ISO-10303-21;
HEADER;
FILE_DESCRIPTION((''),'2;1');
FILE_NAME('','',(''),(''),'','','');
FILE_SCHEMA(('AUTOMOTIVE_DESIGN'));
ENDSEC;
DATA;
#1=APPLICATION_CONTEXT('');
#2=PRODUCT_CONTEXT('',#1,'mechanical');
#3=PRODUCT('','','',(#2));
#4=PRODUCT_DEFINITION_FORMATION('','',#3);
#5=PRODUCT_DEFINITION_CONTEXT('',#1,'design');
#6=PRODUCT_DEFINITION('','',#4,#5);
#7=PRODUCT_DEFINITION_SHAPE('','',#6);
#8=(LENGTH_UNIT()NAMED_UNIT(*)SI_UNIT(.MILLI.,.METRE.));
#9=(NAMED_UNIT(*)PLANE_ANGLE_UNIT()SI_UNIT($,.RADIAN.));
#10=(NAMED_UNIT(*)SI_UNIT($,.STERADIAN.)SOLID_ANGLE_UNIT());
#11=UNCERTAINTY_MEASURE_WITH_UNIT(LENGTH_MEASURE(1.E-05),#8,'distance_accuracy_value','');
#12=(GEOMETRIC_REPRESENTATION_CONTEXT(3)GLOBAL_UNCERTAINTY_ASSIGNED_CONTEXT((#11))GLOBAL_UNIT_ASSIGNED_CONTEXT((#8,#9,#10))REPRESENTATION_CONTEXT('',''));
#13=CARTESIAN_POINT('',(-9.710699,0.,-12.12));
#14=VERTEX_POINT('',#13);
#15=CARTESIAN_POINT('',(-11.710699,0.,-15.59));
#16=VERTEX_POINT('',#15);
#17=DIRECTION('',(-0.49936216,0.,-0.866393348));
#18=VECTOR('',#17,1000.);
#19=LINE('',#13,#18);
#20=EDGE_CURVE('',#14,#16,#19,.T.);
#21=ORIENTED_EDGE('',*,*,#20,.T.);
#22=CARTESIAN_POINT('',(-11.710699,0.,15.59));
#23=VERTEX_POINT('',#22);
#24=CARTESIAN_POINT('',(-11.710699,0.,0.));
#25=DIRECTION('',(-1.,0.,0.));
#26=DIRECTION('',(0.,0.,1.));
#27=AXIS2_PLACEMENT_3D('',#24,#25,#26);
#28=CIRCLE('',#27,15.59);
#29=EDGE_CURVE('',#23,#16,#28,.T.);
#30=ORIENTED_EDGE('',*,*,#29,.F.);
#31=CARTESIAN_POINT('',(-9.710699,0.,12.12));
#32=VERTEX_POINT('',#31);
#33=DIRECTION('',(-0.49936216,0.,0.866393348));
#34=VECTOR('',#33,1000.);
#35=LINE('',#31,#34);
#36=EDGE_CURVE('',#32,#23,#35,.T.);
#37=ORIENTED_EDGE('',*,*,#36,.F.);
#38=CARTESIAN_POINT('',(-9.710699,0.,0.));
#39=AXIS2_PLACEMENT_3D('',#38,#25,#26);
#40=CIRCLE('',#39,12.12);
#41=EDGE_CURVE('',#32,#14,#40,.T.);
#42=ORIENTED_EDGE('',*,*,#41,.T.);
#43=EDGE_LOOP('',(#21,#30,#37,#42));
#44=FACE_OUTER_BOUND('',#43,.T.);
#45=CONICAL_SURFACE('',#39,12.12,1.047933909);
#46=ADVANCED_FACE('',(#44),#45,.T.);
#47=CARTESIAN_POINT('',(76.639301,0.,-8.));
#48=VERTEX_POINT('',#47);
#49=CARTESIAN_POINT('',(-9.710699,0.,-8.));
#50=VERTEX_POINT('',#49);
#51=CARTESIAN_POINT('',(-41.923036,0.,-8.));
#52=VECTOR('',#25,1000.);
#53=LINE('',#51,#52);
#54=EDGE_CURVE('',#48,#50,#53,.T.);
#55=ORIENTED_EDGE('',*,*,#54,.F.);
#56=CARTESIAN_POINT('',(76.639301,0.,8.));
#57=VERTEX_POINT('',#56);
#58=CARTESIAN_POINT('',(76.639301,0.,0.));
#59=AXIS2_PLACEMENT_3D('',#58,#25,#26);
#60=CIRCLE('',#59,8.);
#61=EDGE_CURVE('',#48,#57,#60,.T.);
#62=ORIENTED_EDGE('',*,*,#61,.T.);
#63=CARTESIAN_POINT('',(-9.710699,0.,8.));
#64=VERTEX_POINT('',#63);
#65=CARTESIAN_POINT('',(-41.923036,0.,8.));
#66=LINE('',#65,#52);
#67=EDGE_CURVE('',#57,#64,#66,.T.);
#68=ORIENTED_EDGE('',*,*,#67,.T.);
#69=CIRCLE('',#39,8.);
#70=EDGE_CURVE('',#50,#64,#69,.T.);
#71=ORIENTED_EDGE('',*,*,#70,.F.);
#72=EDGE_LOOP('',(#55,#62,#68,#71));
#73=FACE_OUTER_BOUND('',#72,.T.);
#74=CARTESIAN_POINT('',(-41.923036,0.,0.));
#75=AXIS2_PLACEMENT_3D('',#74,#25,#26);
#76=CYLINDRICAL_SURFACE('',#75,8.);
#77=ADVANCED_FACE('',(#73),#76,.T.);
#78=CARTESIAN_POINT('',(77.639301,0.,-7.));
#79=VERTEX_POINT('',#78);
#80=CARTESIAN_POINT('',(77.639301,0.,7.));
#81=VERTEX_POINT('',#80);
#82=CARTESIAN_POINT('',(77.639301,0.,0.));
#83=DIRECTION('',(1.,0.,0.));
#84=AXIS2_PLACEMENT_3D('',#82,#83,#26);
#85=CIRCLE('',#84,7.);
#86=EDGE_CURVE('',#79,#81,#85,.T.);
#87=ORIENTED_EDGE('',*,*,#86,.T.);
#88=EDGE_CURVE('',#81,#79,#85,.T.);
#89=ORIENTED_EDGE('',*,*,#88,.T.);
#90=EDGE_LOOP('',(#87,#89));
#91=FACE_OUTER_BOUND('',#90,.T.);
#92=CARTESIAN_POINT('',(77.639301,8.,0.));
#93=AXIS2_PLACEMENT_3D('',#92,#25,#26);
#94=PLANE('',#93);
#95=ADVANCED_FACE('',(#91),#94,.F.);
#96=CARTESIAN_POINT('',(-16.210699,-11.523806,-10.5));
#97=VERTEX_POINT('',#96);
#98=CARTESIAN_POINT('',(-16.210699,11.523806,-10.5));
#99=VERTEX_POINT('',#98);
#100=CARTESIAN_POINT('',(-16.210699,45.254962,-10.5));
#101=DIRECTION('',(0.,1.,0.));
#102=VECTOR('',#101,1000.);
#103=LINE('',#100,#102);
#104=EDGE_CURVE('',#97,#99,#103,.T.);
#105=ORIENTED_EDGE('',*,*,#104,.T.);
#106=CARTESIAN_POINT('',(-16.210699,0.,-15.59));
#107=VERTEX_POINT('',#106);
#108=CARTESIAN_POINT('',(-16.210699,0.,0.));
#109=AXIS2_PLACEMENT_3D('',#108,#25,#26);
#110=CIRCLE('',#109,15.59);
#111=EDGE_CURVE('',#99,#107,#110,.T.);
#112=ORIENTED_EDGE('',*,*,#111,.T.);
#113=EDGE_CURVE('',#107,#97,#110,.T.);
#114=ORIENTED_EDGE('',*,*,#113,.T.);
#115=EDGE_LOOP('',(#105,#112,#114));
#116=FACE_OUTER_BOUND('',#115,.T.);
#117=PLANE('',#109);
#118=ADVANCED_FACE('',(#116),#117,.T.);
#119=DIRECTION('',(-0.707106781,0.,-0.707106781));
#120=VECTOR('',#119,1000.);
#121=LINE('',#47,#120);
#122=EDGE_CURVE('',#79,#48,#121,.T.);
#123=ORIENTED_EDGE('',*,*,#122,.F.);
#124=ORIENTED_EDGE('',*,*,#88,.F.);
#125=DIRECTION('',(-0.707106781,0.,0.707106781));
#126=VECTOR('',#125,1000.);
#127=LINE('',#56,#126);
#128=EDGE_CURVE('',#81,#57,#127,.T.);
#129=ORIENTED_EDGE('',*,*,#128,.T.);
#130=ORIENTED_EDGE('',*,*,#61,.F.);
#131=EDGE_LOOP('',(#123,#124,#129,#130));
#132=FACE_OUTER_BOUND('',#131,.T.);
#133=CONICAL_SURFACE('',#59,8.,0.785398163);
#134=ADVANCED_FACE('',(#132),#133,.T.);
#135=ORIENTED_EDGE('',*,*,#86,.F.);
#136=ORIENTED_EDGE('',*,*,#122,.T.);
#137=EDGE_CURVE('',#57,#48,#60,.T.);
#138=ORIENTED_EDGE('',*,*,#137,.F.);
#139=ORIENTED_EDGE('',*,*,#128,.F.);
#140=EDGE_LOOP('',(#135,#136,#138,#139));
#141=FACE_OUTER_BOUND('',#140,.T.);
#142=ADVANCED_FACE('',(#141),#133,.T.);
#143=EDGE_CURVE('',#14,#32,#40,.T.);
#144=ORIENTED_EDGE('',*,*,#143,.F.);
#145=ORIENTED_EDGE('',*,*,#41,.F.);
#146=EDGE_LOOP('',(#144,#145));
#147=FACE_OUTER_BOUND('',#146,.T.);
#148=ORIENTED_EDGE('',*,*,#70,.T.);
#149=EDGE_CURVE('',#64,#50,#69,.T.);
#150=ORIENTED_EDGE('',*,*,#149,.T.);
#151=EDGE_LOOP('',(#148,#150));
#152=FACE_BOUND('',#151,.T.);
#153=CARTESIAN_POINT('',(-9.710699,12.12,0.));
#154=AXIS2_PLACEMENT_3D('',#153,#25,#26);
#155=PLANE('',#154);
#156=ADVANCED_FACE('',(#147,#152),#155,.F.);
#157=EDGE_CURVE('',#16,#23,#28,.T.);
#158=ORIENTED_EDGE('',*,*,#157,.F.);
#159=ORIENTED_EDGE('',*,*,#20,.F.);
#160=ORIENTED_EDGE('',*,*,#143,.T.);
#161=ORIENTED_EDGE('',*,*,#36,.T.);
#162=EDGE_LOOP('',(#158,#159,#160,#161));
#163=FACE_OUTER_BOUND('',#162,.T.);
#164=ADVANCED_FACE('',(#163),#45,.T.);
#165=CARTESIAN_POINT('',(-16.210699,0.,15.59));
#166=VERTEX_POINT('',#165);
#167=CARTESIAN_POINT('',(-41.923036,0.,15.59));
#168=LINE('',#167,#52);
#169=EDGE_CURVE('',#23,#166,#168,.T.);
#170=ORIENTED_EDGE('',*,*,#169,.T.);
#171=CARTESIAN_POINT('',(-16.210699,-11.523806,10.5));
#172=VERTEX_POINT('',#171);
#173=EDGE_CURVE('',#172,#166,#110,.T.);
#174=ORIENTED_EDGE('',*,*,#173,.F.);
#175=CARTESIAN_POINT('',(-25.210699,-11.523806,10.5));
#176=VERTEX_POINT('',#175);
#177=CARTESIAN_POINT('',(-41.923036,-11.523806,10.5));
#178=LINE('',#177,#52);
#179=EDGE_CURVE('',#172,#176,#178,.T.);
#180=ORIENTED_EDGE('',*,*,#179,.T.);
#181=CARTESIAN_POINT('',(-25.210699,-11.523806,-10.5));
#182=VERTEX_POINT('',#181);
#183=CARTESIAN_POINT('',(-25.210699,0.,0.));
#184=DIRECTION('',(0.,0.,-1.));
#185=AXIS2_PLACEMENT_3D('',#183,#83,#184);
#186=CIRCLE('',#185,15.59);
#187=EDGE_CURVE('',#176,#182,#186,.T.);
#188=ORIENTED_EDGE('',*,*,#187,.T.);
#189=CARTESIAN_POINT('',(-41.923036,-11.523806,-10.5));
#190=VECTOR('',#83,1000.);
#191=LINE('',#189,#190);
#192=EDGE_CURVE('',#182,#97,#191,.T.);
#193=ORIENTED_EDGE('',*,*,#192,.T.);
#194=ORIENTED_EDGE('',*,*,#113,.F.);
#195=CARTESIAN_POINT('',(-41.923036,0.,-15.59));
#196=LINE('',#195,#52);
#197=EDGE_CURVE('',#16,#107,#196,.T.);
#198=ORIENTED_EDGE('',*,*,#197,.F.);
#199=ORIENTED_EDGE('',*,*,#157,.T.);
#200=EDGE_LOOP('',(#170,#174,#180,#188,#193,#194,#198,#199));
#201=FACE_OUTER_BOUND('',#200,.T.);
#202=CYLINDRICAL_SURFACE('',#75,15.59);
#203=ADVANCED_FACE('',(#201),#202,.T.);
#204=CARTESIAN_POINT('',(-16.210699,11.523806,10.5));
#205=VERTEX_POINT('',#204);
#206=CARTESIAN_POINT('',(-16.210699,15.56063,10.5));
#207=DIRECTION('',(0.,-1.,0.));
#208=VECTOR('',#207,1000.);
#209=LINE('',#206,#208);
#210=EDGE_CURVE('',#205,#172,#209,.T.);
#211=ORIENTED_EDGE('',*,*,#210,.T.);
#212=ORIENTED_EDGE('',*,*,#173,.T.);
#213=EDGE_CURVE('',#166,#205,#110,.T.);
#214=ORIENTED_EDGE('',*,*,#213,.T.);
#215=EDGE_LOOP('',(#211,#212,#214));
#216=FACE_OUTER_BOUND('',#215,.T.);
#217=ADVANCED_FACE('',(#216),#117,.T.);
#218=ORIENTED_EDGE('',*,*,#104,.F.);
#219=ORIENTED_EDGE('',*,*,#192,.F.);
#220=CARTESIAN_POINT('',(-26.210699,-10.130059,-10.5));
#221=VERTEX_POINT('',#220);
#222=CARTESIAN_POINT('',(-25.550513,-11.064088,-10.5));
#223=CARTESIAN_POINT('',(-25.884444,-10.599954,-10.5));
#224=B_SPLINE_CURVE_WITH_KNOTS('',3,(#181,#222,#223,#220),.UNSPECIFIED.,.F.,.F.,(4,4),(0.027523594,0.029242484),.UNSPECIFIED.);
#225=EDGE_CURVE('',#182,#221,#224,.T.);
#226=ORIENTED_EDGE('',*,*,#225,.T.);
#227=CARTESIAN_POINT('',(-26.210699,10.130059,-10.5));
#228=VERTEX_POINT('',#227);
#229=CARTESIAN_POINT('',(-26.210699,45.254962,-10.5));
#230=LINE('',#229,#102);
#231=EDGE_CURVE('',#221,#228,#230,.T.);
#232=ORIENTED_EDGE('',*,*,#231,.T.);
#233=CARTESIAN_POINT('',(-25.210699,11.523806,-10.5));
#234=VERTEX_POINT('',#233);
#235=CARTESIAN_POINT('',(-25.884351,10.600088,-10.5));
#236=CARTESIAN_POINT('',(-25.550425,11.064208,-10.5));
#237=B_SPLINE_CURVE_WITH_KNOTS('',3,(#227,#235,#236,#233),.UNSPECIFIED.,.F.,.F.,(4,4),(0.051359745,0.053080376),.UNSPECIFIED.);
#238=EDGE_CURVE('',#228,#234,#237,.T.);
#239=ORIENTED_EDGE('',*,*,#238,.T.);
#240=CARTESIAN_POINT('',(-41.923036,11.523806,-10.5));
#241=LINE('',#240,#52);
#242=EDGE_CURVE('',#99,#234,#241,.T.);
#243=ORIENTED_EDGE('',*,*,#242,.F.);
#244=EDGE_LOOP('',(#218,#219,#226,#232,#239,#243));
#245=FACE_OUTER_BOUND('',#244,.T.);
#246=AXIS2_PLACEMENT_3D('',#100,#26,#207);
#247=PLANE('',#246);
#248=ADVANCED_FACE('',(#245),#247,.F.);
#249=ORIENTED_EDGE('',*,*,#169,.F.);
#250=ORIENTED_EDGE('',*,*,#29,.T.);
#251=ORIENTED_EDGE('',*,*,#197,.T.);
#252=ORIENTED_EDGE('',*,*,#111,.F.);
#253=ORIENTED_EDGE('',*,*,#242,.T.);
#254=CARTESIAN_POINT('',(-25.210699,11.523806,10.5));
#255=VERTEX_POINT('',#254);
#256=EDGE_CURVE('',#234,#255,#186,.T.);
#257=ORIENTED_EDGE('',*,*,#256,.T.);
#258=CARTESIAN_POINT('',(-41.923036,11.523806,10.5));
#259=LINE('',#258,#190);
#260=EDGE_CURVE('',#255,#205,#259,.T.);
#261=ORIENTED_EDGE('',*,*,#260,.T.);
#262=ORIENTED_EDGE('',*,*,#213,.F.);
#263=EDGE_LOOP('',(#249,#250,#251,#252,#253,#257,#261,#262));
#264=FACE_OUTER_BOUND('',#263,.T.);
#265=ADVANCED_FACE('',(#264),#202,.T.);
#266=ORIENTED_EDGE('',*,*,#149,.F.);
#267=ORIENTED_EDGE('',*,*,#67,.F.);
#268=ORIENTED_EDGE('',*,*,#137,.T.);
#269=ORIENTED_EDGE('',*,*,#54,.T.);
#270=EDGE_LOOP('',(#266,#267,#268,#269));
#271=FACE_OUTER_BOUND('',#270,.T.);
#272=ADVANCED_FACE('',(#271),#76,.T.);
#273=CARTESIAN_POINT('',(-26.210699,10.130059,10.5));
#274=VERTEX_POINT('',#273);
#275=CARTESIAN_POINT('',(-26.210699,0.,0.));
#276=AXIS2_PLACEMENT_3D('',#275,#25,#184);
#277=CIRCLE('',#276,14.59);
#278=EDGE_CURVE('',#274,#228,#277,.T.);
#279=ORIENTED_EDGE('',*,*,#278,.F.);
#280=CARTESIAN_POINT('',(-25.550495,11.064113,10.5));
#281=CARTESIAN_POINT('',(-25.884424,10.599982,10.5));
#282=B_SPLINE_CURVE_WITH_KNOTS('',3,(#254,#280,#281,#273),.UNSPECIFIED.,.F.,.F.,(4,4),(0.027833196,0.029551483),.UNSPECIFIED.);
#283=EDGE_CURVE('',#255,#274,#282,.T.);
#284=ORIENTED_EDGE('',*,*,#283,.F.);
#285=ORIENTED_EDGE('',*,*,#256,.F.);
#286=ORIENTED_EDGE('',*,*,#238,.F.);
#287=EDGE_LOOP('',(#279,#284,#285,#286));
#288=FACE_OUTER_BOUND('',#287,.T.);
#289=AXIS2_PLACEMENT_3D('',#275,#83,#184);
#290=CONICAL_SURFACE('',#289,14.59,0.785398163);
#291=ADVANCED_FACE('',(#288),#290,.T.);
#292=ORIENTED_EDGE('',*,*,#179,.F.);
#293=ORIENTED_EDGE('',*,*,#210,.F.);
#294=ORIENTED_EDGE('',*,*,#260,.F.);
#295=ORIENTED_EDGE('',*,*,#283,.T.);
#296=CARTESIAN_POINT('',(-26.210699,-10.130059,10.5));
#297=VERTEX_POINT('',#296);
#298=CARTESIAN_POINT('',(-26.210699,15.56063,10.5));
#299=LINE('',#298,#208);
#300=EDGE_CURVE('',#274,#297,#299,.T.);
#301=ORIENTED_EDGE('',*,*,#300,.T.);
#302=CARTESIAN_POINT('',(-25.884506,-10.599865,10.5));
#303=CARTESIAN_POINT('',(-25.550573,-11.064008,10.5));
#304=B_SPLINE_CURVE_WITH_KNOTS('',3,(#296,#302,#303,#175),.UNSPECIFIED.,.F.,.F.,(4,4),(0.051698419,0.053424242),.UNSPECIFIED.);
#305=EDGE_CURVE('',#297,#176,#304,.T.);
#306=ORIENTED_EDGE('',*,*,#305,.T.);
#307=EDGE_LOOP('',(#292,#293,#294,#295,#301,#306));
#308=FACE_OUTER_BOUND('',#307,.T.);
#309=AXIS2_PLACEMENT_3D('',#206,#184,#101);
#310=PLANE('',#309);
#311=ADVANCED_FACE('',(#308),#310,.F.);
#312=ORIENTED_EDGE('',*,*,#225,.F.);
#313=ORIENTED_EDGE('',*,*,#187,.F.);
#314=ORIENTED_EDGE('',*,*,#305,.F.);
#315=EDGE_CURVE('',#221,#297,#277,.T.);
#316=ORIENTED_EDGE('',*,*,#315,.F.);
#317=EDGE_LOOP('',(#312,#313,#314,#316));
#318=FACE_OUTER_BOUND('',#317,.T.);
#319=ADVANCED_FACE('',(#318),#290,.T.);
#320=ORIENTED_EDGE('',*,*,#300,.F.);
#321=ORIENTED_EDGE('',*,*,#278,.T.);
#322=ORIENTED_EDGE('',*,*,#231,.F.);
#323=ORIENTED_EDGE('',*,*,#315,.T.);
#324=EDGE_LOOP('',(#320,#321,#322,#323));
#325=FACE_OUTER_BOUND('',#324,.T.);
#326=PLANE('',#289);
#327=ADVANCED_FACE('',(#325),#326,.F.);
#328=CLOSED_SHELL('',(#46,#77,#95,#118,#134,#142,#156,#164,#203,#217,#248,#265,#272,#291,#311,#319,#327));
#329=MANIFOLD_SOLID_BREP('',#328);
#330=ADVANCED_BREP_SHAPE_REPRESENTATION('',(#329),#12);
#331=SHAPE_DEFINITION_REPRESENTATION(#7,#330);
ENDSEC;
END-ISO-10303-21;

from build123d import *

# Parameters (mm, degrees)
CHAMFER1_SIZE      = 1
CHAMFER2_SIZE      = 1
SKETCH2_W          = 8.284694005
SKETCH2_H          = 60
SKETCH2_W_2        = 10.903172422
SKETCH2_H_2        = 30.692001108
CUT_EXTRUDE1_DEPTH = 10


with BuildPart() as part:
    # Sketch1 → Revolve1 (revolve)
    with BuildSketch(Plane.XY, mode=Mode.PRIVATE) as revolve1_sk:
        Polygon((-26.210699301, 0), (-26.210699301, 15.59), (-11.710699301, 15.59), (-9.710699301, 12.12), (-9.710699301, 8), (77.639300699, 8), (77.639300699, 0), align=None)
    revolve(revolve1_sk.sketch.rotate(Axis((-41.923036121, 0, 0), (1, 0, 0)), 90), axis=Axis((-41.923036121, 0, 0), (1, 0, 0)))

    # Chamfer1
    chamfer1_edges = [part.edges().sort_by_distance(p)[0] for p in [
        (-26.210699301, 0, -15.59),
    ]]
    chamfer(chamfer1_edges, length=CHAMFER1_SIZE)

    # Chamfer2
    chamfer2_edges = [part.edges().sort_by_distance(p)[0] for p in [
        (77.639300699, 0, -8),
    ]]
    chamfer(chamfer2_edges, length=CHAMFER2_SIZE)

    # Sketch2 → Cut-Extrude1 (cut)
    with BuildSketch(Plane.ZY.offset(26.210699301)):
        with Locations((-14.642347003, 15.254961706)):
            Rectangle(SKETCH2_W, SKETCH2_H)
        with Locations((15.951586211, 0.214629378)):
            Rectangle(SKETCH2_W_2, SKETCH2_H_2)
    extrude(amount=-CUT_EXTRUDE1_DEPTH, mode=Mode.SUBTRACT)


solid = part.part
